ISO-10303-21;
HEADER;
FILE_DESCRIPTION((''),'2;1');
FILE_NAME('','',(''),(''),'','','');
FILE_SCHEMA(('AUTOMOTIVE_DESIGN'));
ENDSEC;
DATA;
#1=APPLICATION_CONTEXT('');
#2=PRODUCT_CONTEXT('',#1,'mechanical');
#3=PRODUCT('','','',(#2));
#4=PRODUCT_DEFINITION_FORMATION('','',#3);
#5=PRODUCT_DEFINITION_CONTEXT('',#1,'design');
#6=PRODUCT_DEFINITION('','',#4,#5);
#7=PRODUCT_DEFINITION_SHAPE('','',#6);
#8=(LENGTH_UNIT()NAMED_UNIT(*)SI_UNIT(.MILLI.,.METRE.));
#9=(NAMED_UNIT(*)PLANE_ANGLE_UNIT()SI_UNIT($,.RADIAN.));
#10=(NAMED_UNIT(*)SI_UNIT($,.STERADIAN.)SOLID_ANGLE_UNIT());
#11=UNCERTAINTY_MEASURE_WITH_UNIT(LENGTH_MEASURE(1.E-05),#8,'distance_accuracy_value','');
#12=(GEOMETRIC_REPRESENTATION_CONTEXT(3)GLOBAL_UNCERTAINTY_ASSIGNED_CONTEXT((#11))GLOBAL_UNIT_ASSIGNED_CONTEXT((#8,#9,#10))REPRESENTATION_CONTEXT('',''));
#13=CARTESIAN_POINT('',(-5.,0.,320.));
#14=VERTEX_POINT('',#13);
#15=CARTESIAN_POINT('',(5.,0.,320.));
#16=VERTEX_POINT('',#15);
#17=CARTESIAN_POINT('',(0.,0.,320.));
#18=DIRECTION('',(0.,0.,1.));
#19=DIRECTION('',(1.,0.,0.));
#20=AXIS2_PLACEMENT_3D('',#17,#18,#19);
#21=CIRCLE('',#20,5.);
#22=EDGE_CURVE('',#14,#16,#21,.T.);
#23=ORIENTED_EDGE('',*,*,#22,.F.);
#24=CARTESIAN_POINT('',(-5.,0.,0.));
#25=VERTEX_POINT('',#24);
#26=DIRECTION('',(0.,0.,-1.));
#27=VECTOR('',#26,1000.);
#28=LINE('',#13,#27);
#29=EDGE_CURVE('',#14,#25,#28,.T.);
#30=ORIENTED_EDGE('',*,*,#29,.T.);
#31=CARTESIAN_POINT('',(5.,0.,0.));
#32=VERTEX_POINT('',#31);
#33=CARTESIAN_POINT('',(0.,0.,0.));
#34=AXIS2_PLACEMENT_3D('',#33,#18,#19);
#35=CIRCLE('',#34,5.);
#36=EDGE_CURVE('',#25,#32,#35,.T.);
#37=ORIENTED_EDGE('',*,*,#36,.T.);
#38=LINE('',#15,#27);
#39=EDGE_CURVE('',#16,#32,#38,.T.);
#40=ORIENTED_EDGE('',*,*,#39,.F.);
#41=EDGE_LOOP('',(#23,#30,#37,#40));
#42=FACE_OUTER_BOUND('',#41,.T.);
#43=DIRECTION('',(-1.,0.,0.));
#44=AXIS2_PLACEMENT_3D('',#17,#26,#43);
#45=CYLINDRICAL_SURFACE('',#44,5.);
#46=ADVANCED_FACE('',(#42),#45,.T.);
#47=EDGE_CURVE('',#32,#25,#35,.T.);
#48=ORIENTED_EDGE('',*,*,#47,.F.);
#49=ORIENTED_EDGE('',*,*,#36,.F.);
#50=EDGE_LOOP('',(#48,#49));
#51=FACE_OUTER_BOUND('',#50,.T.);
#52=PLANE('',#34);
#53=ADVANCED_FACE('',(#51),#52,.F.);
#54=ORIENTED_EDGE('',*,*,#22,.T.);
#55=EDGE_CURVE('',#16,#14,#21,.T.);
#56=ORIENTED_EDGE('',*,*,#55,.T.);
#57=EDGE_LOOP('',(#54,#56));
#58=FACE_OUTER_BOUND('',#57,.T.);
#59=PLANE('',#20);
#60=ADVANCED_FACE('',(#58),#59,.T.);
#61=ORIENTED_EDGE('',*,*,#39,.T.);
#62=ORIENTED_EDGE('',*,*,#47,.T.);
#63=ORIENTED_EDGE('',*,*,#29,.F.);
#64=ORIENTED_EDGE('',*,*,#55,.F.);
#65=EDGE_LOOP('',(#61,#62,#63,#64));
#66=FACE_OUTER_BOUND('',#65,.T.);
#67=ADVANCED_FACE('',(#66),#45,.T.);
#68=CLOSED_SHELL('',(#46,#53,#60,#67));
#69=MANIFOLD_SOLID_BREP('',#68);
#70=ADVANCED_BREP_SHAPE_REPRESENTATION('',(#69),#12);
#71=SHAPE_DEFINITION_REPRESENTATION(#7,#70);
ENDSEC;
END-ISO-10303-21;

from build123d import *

# Parameters (mm, degrees)
SKETCH1_R           = 5
BOSS_EXTRUDE1_DEPTH = 320


with BuildPart() as part:
    # Sketch1 → Boss-Extrude1 (new body)
    with BuildSketch(Plane.XY):
        with Locations(Location((0, 0, 0), (0, 0, 180))):
            Circle(SKETCH1_R)
    extrude(amount=BOSS_EXTRUDE1_DEPTH)


solid = part.part
